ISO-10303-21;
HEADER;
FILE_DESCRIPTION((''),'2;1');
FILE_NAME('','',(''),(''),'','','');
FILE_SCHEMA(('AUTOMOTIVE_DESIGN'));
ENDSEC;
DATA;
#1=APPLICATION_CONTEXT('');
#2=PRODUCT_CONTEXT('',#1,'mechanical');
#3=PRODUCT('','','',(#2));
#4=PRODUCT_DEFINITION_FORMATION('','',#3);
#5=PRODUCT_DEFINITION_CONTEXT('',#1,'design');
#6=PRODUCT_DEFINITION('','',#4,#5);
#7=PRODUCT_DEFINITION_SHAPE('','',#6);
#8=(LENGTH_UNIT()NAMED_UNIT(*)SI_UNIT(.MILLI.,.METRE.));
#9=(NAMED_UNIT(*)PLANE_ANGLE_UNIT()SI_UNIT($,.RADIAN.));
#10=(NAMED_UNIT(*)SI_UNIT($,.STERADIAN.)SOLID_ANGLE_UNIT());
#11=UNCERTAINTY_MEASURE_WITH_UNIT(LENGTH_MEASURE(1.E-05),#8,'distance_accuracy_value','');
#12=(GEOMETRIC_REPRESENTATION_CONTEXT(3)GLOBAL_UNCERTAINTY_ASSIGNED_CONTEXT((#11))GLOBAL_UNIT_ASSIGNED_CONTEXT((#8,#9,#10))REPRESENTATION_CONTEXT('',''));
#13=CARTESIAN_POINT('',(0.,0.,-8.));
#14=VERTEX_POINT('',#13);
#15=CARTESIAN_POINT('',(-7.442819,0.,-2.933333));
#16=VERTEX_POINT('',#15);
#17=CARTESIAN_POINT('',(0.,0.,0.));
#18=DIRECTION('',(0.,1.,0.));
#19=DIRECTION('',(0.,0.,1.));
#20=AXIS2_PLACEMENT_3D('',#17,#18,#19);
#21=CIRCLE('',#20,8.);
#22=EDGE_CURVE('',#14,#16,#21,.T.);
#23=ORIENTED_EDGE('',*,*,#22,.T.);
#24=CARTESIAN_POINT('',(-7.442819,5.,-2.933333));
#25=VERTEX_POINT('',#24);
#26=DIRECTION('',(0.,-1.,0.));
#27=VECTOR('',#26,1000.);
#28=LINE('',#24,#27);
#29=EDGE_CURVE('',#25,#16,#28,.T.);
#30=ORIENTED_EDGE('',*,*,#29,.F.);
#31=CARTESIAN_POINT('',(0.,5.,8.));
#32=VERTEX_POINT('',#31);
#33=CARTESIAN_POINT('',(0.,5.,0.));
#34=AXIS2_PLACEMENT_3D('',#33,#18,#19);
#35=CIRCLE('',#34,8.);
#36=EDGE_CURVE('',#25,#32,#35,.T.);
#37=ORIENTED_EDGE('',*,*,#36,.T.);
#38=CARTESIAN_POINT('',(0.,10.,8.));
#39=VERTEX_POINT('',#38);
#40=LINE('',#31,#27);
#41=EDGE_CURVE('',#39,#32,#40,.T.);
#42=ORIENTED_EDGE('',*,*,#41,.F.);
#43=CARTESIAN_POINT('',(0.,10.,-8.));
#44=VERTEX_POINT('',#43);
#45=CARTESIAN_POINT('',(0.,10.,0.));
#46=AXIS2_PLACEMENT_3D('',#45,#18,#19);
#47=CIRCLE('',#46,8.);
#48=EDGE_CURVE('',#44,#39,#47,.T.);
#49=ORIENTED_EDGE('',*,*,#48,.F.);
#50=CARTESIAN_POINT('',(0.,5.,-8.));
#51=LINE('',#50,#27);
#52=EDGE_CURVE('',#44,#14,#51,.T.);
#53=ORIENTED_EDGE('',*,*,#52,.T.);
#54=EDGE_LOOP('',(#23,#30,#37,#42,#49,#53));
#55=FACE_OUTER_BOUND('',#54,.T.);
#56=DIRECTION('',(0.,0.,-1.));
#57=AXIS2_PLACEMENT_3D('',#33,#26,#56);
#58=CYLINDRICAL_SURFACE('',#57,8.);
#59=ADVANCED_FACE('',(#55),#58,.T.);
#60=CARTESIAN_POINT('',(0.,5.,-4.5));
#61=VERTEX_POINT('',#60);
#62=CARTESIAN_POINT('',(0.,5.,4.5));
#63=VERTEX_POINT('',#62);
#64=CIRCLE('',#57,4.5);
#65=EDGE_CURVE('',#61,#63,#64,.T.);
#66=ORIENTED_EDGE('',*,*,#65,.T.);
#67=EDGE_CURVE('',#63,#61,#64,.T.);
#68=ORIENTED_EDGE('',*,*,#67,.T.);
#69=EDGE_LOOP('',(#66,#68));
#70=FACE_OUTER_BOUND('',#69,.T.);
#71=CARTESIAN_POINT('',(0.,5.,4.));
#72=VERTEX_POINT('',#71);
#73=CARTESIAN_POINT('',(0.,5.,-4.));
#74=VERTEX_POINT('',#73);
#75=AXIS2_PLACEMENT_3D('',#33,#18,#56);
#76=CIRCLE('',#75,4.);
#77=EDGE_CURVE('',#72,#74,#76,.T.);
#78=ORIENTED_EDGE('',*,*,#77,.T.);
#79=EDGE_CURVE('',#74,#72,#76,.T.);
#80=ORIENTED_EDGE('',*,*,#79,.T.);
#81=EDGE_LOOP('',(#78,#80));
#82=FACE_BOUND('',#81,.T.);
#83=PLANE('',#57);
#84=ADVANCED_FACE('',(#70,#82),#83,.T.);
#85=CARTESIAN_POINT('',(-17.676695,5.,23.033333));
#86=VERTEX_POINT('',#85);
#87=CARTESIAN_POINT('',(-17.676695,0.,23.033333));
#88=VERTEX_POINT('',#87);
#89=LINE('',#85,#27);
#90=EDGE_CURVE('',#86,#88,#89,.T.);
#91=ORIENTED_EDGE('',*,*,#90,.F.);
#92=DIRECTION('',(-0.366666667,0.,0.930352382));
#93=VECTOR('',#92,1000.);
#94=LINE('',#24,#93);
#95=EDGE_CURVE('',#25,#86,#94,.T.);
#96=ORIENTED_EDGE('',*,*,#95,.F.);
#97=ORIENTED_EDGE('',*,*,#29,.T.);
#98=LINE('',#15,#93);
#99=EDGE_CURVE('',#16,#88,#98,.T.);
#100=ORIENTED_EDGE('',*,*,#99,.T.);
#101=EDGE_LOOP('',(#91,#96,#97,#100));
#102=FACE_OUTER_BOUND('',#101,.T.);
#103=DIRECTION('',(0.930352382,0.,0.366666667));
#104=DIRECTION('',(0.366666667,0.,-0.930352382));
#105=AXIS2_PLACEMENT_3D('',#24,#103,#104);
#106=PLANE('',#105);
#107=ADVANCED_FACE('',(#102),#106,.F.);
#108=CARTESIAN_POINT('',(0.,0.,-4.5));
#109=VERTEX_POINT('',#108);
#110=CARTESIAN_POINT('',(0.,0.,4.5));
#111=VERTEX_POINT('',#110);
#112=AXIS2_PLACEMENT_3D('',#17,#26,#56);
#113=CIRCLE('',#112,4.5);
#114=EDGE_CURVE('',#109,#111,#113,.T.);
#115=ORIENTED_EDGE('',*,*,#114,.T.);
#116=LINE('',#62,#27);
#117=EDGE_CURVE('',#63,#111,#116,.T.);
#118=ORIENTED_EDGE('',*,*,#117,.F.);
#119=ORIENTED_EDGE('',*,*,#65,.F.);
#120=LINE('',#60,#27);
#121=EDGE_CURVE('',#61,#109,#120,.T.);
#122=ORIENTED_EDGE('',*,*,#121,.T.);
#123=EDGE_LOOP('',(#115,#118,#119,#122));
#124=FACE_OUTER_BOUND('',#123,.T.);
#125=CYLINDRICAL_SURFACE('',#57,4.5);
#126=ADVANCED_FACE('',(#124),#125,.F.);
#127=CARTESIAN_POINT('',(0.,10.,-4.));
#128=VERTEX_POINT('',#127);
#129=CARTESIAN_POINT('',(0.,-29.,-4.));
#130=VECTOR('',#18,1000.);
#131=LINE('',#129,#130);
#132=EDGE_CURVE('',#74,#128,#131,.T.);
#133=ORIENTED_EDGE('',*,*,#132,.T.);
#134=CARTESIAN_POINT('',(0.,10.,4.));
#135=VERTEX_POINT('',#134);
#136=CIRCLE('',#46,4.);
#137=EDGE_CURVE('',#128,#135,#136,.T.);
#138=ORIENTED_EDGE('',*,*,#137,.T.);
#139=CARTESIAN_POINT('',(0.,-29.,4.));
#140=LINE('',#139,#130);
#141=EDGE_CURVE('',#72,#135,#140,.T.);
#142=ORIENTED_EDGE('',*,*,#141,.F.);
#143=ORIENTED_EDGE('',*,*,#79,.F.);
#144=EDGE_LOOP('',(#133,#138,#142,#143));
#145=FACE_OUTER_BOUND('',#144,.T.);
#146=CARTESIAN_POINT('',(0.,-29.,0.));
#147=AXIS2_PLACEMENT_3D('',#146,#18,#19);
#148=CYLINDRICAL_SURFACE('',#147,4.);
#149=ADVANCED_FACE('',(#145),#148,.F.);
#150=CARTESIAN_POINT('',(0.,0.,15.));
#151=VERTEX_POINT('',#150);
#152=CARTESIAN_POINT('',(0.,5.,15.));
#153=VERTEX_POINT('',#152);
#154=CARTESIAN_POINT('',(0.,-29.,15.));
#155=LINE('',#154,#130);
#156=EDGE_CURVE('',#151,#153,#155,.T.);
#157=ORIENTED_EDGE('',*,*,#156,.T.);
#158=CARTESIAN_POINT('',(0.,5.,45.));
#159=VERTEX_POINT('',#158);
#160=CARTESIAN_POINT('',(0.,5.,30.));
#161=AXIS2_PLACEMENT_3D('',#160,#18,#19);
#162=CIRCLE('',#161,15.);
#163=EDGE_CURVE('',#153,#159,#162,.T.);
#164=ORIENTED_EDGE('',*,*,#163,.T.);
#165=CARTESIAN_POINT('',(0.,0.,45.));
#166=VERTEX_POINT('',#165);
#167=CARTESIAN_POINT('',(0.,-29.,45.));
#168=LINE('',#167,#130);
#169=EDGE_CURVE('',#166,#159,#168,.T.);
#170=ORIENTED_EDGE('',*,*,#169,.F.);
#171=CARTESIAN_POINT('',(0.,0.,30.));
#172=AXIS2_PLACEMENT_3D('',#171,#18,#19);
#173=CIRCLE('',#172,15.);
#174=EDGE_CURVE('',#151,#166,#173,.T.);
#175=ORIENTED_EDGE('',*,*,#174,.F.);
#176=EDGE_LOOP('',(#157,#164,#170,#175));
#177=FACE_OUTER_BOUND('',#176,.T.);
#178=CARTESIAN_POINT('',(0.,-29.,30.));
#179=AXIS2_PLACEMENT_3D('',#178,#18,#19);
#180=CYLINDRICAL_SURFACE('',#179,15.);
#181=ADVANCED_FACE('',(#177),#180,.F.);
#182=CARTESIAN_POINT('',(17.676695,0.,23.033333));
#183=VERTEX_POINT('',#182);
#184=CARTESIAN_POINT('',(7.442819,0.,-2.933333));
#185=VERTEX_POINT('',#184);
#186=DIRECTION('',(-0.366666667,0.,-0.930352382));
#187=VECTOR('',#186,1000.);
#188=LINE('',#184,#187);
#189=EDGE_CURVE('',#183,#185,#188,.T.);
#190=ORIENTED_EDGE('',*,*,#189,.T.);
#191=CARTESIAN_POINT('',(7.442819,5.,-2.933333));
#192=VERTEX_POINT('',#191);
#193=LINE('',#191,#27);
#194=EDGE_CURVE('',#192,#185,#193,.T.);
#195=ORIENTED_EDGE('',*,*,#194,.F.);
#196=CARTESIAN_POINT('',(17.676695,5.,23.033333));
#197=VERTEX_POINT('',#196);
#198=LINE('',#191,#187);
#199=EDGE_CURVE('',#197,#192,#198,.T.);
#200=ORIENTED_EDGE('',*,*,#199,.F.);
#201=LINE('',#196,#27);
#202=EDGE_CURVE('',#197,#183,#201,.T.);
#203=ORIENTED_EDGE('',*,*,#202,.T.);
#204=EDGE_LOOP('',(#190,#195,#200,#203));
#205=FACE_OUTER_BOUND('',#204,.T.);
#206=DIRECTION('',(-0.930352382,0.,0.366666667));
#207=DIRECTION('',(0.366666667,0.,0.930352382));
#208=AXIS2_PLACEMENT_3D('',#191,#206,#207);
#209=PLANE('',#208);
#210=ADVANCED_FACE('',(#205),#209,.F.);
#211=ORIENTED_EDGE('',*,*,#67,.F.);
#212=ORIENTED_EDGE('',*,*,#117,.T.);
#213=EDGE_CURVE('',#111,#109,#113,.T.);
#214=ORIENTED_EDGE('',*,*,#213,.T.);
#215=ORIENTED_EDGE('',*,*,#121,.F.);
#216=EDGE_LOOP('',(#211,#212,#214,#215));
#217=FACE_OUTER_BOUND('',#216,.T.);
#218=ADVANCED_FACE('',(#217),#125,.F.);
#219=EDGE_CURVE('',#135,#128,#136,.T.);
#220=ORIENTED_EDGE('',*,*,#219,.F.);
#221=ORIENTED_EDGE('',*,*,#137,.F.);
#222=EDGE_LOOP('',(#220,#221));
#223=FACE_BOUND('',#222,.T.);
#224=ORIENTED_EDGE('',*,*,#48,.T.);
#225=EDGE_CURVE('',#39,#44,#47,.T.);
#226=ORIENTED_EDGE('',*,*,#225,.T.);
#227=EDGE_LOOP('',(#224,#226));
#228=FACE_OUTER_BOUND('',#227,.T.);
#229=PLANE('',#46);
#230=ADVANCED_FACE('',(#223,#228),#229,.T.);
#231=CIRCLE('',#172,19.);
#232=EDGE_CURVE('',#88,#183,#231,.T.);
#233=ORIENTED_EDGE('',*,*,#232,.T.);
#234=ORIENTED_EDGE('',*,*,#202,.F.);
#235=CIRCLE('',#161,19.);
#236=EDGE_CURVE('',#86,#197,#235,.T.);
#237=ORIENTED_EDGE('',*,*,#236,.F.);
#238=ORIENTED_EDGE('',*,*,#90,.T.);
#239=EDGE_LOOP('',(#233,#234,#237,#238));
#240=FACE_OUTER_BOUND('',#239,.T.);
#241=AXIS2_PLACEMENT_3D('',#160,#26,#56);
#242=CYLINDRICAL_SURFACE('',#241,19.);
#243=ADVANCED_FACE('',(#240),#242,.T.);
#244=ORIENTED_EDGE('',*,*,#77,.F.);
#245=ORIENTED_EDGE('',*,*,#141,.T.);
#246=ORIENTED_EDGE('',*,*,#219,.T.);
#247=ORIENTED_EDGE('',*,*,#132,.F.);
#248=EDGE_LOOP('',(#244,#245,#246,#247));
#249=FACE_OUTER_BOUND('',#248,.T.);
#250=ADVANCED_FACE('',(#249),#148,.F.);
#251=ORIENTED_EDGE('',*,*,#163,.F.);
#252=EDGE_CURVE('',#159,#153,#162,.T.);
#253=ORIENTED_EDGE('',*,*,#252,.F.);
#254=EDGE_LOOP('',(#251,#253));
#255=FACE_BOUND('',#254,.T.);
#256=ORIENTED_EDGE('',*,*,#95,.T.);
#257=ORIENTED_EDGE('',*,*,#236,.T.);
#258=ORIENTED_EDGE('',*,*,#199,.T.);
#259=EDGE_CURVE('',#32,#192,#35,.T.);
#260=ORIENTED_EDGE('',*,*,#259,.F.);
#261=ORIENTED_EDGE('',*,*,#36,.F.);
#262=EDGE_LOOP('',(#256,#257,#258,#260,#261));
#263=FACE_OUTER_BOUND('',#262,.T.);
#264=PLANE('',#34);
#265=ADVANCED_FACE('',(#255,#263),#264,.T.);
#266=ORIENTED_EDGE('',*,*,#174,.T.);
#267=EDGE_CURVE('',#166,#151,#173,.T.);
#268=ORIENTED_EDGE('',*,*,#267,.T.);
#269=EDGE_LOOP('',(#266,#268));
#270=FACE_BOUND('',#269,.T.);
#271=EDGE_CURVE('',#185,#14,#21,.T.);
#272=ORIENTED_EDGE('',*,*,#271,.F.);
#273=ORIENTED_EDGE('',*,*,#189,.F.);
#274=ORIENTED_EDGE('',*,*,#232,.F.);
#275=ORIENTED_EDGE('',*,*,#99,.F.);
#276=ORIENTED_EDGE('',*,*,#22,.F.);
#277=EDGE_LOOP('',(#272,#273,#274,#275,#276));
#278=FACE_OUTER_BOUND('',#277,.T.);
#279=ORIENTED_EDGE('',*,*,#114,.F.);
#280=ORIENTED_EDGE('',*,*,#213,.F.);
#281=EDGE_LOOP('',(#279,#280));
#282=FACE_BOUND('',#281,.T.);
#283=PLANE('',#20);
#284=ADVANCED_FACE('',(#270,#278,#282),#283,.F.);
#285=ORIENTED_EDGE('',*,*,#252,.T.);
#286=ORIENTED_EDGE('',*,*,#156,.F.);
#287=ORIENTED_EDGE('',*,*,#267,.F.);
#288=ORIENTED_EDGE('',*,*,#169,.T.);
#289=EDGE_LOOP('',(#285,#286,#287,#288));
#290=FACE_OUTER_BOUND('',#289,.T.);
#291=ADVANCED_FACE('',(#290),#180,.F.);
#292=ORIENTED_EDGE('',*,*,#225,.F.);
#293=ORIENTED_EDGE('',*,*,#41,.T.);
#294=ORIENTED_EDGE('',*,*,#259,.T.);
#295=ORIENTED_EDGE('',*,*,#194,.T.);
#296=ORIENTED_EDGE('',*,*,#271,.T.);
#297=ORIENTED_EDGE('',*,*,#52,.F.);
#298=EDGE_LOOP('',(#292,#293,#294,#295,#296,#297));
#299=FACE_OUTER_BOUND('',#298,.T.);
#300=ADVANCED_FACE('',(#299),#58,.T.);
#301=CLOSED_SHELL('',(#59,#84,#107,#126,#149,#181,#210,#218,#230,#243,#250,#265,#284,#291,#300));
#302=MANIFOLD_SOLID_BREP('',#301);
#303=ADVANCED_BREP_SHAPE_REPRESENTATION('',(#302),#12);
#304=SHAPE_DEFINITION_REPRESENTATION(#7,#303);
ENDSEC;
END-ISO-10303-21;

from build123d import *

# Parameters (mm, degrees)
BOSS_EXTRUDE1_DEPTH = 5
SKETCH2_R           = 8
BOSS_EXTRUDE2_DEPTH = 5
SKETCH3_R           = 4
SKETCH3_R_2         = 15
CUT_EXTRUDE1_DEPTH  = 39
SKETCH4_R           = 4.5
CUT_EXTRUDE2_DEPTH  = 5


with BuildPart() as part:
    # Sketch1 → Boss-Extrude1 (new body)
    with BuildSketch(Plane(origin=(0, 0, 0), x_dir=(1, 0, 0), z_dir=(0, 1, 0))):
        with BuildLine():
            Line((-7.44281906, 2.933333333), (-17.676695267, -23.033333333))
            ThreePointArc((-17.676695267, -23.033333333), (0, -49), (17.676695267, -23.033333333))
            Line((17.676695267, -23.033333333), (7.44281906, 2.933333333))
            ThreePointArc((7.44281906, 2.933333333), (0, 8), (-7.44281906, 2.933333333))
        make_face()
    extrude(amount=BOSS_EXTRUDE1_DEPTH)

    # Sketch2 → Boss-Extrude2 (add)
    with BuildSketch(Plane(origin=(0, 5, 0), x_dir=(1, 0, 0), z_dir=(0, 1, 0))):
        with Locations(Location((0, 0, 0), (0, 0, 158.489811733))):
            Circle(SKETCH2_R)
    extrude(amount=BOSS_EXTRUDE2_DEPTH)

    # Sketch3 → Cut-Extrude1 (cut)
    with BuildSketch(Plane(origin=(0, 10, 0), x_dir=(1, 0, 0), z_dir=(0, 1, 0))):
        with Locations(Location((0, 0, 0), (0, 0, 270))):
            Circle(SKETCH3_R)
        with Locations(Location((0, -30, 0), (0, 0, 270))):
            Circle(SKETCH3_R_2)
    extrude(amount=-CUT_EXTRUDE1_DEPTH, mode=Mode.SUBTRACT)

    # Sketch4 → Cut-Extrude2 (cut)
    with BuildSketch(Plane.XZ):
        with Locations(Location((0, 0, 0), (0, 0, 270))):
            Circle(SKETCH4_R)
    extrude(amount=-CUT_EXTRUDE2_DEPTH, mode=Mode.SUBTRACT)


solid = part.part
